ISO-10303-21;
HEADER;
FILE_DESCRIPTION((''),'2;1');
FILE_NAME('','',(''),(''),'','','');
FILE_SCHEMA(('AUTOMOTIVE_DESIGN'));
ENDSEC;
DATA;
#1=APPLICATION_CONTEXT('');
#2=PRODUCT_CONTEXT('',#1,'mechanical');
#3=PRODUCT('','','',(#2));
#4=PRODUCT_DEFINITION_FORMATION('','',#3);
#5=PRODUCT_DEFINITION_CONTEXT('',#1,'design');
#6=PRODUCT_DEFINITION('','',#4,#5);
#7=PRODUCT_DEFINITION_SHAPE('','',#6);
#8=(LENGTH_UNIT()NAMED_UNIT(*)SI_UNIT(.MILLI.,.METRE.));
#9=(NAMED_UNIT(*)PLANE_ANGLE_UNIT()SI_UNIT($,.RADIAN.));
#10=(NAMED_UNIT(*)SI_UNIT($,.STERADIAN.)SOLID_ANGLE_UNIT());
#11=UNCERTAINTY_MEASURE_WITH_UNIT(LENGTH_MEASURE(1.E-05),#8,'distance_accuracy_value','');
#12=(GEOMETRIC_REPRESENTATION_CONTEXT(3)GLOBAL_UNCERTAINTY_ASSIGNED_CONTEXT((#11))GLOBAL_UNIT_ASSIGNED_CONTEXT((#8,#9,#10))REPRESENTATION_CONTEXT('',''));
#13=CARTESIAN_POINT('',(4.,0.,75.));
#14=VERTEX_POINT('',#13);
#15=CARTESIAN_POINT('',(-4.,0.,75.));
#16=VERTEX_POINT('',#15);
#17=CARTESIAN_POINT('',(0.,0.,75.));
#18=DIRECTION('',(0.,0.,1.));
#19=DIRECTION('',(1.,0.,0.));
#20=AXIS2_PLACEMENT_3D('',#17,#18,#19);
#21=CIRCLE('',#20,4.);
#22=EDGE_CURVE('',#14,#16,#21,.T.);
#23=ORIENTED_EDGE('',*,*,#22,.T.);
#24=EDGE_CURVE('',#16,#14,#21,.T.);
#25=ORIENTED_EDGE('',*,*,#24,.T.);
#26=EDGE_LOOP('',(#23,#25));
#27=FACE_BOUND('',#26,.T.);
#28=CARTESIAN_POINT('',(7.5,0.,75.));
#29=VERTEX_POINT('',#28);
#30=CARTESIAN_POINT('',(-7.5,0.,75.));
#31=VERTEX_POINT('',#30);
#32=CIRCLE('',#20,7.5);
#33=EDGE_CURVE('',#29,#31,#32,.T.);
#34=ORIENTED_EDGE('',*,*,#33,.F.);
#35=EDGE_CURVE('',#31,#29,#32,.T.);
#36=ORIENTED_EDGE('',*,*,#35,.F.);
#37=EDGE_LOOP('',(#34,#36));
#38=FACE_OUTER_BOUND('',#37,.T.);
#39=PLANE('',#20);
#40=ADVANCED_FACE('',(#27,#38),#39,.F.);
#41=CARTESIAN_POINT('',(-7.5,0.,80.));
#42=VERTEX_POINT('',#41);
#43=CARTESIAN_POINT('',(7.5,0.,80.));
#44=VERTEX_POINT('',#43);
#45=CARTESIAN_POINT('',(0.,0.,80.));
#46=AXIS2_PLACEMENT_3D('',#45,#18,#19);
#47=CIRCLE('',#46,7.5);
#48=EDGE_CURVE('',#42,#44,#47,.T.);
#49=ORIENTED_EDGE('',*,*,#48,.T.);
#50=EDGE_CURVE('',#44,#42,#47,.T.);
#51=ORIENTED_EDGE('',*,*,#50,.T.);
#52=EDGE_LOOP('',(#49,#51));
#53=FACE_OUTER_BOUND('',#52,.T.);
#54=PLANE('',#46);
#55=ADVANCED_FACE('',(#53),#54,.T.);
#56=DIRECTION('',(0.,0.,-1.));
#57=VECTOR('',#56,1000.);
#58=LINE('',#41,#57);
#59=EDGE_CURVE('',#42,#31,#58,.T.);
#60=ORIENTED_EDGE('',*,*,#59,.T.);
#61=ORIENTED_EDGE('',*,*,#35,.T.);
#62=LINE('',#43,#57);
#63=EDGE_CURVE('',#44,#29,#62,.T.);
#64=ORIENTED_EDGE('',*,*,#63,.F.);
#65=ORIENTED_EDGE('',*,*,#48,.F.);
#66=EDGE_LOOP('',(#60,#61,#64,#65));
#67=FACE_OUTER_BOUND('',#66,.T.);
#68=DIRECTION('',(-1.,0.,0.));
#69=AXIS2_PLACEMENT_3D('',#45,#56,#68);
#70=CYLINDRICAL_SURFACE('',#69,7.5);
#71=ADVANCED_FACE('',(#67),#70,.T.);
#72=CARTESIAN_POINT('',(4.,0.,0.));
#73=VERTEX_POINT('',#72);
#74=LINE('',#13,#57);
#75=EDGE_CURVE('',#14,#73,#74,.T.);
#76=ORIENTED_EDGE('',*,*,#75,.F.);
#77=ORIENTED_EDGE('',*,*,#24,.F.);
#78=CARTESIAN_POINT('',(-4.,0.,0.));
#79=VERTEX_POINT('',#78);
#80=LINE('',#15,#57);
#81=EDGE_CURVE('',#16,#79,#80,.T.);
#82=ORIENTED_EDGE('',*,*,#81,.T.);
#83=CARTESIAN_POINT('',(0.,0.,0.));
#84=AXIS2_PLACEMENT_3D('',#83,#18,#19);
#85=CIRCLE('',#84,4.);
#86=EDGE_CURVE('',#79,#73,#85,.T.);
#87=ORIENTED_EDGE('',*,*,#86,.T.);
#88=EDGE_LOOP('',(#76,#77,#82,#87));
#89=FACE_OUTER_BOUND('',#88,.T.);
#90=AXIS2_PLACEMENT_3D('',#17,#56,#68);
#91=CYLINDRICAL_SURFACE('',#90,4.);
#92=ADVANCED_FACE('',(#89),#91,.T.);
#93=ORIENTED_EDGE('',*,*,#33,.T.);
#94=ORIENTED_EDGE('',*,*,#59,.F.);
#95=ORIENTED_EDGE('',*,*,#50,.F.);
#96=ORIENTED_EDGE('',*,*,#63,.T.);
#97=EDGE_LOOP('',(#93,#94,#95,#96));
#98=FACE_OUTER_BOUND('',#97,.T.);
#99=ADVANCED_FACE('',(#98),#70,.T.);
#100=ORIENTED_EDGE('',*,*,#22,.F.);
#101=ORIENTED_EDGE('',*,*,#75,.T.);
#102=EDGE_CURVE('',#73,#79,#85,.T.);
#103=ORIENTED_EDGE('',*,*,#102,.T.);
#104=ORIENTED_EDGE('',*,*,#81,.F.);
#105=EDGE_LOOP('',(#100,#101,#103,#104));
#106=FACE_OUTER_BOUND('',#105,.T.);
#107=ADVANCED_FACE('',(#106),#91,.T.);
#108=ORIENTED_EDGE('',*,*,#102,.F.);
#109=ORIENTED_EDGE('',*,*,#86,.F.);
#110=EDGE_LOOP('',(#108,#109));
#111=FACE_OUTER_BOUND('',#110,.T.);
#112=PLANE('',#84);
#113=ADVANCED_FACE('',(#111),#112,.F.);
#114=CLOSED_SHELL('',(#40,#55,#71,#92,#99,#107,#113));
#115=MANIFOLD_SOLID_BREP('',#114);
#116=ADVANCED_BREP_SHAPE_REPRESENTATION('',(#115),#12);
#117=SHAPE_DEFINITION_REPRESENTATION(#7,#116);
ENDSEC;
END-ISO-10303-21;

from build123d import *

# Parameters (mm, degrees)
SKETCH1_R           = 4
BOSS_EXTRUDE1_DEPTH = 75
SKETCH2_R           = 7.5
BOSS_EXTRUDE2_DEPTH = 5


with BuildPart() as part:
    # Sketch1 → Boss-Extrude1 (new body)
    with BuildSketch(Plane.XY):
        Circle(SKETCH1_R)
    extrude(amount=BOSS_EXTRUDE1_DEPTH)

    # Sketch2 → Boss-Extrude2 (add)
    with BuildSketch(Plane.XY.offset(75)):
        Circle(SKETCH2_R)
    extrude(amount=BOSS_EXTRUDE2_DEPTH)


solid = part.part
